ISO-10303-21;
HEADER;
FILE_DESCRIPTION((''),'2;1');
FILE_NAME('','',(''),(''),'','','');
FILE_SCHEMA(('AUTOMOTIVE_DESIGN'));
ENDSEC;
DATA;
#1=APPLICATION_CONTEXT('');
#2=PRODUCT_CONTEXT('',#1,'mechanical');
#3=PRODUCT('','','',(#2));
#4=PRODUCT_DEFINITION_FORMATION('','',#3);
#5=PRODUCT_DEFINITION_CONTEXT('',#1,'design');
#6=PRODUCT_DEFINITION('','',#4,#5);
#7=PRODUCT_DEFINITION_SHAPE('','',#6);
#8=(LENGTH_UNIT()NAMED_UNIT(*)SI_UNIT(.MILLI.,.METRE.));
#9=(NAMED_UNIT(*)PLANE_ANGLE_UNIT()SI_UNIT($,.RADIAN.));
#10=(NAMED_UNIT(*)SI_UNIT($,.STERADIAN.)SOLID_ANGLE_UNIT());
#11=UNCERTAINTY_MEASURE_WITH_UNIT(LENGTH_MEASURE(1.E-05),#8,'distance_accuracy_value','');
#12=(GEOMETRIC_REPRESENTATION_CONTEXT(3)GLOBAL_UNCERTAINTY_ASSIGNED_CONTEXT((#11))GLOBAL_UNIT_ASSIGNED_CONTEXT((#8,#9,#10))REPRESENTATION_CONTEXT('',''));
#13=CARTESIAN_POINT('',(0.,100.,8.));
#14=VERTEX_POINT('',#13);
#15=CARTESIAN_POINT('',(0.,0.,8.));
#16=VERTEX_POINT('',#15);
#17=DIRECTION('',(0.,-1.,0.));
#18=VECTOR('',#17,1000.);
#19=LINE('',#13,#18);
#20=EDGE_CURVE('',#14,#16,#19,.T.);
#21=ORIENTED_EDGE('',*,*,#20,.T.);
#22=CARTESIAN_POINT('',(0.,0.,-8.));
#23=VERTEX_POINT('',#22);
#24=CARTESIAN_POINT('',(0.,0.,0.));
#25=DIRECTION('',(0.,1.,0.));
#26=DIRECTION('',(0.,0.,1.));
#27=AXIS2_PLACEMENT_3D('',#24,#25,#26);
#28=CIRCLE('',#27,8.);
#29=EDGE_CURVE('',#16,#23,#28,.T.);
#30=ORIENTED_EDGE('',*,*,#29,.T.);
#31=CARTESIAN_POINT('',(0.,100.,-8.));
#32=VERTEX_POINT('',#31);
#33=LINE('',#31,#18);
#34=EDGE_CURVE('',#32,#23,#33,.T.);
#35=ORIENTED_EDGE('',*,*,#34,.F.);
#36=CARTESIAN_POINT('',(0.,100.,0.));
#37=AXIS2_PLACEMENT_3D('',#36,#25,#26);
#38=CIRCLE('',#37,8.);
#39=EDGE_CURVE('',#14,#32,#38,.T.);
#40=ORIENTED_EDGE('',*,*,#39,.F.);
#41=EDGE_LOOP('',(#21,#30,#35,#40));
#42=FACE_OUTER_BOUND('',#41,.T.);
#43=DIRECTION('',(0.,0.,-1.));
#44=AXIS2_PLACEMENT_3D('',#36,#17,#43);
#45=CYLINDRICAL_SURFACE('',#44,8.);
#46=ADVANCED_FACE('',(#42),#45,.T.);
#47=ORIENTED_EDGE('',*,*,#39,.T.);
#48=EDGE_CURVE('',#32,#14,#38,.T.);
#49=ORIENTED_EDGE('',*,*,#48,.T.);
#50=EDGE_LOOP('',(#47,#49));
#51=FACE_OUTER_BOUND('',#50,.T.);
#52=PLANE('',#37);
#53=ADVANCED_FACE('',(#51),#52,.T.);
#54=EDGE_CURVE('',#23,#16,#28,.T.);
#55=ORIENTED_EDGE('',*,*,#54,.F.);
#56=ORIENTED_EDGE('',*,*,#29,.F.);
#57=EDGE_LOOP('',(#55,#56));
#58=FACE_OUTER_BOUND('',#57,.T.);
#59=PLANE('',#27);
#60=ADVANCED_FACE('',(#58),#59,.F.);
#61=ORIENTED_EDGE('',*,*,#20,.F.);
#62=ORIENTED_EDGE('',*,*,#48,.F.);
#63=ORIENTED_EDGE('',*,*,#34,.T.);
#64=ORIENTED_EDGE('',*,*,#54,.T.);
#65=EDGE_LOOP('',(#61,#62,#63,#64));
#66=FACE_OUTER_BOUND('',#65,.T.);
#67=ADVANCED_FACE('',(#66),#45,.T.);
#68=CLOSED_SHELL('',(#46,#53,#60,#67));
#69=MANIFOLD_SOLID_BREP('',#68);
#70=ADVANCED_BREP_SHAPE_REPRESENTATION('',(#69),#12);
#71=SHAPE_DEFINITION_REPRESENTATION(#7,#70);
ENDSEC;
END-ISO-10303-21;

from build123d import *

# Parameters (mm, degrees)
SKETCH1_R           = 8
BOSS_EXTRUDE1_DEPTH = 100


with BuildPart() as part:
    # Sketch1 → Boss-Extrude1 (new body)
    with BuildSketch(Plane(origin=(0, 0, 0), x_dir=(1, 0, 0), z_dir=(0, 1, 0))):
        with Locations(Location((0, 0, 0), (0, 0, 270))):
            Circle(SKETCH1_R)
    extrude(amount=BOSS_EXTRUDE1_DEPTH)


solid = part.part
